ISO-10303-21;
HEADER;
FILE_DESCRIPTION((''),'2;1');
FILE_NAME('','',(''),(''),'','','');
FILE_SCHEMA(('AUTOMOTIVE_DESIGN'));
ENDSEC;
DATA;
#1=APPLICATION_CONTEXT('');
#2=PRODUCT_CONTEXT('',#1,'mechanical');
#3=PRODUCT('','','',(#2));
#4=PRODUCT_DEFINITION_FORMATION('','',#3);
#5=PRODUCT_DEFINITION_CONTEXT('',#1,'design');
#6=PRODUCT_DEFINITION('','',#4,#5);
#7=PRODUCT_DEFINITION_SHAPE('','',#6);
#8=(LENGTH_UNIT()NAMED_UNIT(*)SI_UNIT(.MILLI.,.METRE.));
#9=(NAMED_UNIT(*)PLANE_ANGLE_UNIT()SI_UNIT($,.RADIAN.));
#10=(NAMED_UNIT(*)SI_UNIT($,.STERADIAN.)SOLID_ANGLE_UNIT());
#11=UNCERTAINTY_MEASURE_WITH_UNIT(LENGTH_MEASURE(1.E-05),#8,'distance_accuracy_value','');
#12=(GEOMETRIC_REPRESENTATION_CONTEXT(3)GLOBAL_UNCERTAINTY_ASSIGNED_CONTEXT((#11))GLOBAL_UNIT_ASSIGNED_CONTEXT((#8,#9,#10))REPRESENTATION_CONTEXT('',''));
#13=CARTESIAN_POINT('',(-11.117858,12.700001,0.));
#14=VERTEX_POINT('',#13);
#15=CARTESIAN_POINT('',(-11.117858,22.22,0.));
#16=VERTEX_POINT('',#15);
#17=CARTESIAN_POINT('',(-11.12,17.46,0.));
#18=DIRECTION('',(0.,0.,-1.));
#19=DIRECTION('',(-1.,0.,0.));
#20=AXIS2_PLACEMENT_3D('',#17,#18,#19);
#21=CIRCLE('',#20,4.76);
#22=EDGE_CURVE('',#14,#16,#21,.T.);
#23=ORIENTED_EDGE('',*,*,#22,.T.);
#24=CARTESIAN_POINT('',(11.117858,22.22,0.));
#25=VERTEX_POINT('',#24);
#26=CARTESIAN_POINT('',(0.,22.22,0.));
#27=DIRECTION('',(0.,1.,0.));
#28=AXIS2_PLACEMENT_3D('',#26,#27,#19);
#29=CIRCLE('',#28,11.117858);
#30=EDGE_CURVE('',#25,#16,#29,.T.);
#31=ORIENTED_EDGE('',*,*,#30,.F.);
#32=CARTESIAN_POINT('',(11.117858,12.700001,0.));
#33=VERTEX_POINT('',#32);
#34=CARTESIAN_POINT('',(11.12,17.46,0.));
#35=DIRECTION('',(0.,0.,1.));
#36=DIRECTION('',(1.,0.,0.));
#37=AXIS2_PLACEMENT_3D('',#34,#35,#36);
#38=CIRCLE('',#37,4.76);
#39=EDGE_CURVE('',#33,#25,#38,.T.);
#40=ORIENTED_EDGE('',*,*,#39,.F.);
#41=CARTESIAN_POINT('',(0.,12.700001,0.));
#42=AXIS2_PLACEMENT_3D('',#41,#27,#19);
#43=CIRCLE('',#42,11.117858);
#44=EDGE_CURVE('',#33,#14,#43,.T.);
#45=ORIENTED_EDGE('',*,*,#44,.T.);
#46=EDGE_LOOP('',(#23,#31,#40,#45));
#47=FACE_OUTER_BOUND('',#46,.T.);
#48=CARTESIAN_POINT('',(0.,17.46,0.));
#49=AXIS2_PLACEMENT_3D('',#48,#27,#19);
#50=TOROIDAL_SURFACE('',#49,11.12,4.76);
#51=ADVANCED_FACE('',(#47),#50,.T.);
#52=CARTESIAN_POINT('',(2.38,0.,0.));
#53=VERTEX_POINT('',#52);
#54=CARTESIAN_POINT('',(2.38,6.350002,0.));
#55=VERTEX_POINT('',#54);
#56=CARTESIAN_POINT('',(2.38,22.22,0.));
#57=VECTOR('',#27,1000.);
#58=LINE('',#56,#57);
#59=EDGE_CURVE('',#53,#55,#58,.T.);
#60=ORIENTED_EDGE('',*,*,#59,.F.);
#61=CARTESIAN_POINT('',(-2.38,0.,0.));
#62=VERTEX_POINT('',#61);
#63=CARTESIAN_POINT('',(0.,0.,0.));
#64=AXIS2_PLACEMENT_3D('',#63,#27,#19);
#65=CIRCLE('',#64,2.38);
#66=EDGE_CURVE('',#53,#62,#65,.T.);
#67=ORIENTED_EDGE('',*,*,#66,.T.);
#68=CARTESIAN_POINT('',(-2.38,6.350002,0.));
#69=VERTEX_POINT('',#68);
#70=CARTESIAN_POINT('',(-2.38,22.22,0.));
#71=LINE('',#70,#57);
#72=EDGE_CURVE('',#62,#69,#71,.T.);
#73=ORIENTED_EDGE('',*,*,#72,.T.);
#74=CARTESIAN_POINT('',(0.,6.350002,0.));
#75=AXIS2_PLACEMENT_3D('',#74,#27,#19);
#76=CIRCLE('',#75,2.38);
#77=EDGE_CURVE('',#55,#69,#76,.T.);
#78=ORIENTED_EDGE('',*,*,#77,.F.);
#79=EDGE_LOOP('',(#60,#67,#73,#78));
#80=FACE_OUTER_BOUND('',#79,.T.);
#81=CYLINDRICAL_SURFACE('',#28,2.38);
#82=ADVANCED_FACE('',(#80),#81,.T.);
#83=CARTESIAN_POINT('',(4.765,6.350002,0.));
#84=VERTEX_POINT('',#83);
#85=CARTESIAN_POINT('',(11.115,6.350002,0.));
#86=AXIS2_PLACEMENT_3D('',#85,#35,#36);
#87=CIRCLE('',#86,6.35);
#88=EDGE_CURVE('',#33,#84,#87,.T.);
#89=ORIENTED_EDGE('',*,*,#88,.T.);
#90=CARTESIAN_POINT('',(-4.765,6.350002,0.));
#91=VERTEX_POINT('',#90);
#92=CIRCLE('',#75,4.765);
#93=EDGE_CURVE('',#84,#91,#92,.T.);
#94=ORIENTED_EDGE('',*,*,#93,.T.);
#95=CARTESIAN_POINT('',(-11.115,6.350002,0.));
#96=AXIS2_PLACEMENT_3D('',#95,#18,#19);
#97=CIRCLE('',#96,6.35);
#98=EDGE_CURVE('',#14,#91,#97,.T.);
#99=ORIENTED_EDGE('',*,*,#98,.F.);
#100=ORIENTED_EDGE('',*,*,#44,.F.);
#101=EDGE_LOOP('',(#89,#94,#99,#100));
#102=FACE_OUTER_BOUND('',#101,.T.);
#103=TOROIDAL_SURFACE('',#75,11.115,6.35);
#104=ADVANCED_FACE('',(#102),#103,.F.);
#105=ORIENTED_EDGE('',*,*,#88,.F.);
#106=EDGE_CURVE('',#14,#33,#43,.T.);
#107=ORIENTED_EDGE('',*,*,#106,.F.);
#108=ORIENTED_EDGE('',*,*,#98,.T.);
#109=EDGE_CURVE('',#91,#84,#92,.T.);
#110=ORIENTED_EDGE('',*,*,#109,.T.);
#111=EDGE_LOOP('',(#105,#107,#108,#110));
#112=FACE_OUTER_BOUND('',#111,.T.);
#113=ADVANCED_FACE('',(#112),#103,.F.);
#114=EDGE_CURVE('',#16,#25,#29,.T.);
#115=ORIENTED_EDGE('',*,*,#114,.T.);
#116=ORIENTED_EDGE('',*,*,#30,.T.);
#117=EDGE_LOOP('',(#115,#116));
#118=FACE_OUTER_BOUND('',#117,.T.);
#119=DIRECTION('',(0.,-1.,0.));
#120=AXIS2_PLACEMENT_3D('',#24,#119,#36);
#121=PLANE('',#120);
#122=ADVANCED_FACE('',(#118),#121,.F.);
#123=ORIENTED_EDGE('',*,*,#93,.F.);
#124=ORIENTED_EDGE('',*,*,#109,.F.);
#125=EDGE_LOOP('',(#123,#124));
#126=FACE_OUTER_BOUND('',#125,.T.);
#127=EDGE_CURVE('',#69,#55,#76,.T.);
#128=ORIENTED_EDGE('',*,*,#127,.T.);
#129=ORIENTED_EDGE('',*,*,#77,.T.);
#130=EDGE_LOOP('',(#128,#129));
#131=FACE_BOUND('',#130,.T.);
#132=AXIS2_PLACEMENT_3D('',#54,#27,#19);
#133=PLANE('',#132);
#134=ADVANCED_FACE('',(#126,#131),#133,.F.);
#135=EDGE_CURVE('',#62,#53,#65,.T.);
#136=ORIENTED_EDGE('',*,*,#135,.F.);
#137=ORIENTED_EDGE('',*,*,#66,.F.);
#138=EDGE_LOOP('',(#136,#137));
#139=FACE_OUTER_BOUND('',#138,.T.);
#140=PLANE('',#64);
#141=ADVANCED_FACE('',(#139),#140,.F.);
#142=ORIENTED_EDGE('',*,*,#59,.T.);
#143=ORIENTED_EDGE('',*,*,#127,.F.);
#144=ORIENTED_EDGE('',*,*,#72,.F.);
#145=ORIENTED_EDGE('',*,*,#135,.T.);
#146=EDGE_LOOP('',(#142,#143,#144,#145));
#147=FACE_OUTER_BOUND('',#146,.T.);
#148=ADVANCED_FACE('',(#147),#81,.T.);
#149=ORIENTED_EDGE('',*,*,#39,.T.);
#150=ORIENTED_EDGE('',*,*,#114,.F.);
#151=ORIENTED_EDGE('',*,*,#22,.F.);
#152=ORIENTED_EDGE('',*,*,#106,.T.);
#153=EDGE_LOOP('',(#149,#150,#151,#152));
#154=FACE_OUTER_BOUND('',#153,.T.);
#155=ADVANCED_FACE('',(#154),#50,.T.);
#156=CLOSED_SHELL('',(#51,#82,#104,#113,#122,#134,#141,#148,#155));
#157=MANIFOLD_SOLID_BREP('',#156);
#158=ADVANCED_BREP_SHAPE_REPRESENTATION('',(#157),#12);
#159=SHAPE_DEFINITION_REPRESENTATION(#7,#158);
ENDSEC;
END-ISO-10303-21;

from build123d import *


with BuildPart() as part:
    # Knob Profile Sketch → Knob Body Revolve (revolve)
    with BuildSketch(Plane.XY, mode=Mode.PRIVATE) as knob_body_revolve_sk:
        with BuildLine():
            Line((0, 0), (2.38, 0))
            Line((2.38, 0), (2.38, 6.350001607))
            Line((2.38, 6.350001607), (4.765, 6.350001607))
            ThreePointArc((4.765, 6.350001607), (6.625882433, 10.841139934), (11.117857786, 12.700000964))
            ThreePointArc((11.117857786, 12.700000964), (15.88, 17.460000482), (11.117857786, 22.22))
            Line((11.117857786, 22.22), (0, 22.22))
            Line((0, 22.22), (0, 0))
        make_face()
    revolve(knob_body_revolve_sk.sketch.rotate(Axis((0, 22.22, 0), (0, -1, 0)), 180), axis=Axis((0, 22.22, 0), (0, -1, 0)))


solid = part.part
